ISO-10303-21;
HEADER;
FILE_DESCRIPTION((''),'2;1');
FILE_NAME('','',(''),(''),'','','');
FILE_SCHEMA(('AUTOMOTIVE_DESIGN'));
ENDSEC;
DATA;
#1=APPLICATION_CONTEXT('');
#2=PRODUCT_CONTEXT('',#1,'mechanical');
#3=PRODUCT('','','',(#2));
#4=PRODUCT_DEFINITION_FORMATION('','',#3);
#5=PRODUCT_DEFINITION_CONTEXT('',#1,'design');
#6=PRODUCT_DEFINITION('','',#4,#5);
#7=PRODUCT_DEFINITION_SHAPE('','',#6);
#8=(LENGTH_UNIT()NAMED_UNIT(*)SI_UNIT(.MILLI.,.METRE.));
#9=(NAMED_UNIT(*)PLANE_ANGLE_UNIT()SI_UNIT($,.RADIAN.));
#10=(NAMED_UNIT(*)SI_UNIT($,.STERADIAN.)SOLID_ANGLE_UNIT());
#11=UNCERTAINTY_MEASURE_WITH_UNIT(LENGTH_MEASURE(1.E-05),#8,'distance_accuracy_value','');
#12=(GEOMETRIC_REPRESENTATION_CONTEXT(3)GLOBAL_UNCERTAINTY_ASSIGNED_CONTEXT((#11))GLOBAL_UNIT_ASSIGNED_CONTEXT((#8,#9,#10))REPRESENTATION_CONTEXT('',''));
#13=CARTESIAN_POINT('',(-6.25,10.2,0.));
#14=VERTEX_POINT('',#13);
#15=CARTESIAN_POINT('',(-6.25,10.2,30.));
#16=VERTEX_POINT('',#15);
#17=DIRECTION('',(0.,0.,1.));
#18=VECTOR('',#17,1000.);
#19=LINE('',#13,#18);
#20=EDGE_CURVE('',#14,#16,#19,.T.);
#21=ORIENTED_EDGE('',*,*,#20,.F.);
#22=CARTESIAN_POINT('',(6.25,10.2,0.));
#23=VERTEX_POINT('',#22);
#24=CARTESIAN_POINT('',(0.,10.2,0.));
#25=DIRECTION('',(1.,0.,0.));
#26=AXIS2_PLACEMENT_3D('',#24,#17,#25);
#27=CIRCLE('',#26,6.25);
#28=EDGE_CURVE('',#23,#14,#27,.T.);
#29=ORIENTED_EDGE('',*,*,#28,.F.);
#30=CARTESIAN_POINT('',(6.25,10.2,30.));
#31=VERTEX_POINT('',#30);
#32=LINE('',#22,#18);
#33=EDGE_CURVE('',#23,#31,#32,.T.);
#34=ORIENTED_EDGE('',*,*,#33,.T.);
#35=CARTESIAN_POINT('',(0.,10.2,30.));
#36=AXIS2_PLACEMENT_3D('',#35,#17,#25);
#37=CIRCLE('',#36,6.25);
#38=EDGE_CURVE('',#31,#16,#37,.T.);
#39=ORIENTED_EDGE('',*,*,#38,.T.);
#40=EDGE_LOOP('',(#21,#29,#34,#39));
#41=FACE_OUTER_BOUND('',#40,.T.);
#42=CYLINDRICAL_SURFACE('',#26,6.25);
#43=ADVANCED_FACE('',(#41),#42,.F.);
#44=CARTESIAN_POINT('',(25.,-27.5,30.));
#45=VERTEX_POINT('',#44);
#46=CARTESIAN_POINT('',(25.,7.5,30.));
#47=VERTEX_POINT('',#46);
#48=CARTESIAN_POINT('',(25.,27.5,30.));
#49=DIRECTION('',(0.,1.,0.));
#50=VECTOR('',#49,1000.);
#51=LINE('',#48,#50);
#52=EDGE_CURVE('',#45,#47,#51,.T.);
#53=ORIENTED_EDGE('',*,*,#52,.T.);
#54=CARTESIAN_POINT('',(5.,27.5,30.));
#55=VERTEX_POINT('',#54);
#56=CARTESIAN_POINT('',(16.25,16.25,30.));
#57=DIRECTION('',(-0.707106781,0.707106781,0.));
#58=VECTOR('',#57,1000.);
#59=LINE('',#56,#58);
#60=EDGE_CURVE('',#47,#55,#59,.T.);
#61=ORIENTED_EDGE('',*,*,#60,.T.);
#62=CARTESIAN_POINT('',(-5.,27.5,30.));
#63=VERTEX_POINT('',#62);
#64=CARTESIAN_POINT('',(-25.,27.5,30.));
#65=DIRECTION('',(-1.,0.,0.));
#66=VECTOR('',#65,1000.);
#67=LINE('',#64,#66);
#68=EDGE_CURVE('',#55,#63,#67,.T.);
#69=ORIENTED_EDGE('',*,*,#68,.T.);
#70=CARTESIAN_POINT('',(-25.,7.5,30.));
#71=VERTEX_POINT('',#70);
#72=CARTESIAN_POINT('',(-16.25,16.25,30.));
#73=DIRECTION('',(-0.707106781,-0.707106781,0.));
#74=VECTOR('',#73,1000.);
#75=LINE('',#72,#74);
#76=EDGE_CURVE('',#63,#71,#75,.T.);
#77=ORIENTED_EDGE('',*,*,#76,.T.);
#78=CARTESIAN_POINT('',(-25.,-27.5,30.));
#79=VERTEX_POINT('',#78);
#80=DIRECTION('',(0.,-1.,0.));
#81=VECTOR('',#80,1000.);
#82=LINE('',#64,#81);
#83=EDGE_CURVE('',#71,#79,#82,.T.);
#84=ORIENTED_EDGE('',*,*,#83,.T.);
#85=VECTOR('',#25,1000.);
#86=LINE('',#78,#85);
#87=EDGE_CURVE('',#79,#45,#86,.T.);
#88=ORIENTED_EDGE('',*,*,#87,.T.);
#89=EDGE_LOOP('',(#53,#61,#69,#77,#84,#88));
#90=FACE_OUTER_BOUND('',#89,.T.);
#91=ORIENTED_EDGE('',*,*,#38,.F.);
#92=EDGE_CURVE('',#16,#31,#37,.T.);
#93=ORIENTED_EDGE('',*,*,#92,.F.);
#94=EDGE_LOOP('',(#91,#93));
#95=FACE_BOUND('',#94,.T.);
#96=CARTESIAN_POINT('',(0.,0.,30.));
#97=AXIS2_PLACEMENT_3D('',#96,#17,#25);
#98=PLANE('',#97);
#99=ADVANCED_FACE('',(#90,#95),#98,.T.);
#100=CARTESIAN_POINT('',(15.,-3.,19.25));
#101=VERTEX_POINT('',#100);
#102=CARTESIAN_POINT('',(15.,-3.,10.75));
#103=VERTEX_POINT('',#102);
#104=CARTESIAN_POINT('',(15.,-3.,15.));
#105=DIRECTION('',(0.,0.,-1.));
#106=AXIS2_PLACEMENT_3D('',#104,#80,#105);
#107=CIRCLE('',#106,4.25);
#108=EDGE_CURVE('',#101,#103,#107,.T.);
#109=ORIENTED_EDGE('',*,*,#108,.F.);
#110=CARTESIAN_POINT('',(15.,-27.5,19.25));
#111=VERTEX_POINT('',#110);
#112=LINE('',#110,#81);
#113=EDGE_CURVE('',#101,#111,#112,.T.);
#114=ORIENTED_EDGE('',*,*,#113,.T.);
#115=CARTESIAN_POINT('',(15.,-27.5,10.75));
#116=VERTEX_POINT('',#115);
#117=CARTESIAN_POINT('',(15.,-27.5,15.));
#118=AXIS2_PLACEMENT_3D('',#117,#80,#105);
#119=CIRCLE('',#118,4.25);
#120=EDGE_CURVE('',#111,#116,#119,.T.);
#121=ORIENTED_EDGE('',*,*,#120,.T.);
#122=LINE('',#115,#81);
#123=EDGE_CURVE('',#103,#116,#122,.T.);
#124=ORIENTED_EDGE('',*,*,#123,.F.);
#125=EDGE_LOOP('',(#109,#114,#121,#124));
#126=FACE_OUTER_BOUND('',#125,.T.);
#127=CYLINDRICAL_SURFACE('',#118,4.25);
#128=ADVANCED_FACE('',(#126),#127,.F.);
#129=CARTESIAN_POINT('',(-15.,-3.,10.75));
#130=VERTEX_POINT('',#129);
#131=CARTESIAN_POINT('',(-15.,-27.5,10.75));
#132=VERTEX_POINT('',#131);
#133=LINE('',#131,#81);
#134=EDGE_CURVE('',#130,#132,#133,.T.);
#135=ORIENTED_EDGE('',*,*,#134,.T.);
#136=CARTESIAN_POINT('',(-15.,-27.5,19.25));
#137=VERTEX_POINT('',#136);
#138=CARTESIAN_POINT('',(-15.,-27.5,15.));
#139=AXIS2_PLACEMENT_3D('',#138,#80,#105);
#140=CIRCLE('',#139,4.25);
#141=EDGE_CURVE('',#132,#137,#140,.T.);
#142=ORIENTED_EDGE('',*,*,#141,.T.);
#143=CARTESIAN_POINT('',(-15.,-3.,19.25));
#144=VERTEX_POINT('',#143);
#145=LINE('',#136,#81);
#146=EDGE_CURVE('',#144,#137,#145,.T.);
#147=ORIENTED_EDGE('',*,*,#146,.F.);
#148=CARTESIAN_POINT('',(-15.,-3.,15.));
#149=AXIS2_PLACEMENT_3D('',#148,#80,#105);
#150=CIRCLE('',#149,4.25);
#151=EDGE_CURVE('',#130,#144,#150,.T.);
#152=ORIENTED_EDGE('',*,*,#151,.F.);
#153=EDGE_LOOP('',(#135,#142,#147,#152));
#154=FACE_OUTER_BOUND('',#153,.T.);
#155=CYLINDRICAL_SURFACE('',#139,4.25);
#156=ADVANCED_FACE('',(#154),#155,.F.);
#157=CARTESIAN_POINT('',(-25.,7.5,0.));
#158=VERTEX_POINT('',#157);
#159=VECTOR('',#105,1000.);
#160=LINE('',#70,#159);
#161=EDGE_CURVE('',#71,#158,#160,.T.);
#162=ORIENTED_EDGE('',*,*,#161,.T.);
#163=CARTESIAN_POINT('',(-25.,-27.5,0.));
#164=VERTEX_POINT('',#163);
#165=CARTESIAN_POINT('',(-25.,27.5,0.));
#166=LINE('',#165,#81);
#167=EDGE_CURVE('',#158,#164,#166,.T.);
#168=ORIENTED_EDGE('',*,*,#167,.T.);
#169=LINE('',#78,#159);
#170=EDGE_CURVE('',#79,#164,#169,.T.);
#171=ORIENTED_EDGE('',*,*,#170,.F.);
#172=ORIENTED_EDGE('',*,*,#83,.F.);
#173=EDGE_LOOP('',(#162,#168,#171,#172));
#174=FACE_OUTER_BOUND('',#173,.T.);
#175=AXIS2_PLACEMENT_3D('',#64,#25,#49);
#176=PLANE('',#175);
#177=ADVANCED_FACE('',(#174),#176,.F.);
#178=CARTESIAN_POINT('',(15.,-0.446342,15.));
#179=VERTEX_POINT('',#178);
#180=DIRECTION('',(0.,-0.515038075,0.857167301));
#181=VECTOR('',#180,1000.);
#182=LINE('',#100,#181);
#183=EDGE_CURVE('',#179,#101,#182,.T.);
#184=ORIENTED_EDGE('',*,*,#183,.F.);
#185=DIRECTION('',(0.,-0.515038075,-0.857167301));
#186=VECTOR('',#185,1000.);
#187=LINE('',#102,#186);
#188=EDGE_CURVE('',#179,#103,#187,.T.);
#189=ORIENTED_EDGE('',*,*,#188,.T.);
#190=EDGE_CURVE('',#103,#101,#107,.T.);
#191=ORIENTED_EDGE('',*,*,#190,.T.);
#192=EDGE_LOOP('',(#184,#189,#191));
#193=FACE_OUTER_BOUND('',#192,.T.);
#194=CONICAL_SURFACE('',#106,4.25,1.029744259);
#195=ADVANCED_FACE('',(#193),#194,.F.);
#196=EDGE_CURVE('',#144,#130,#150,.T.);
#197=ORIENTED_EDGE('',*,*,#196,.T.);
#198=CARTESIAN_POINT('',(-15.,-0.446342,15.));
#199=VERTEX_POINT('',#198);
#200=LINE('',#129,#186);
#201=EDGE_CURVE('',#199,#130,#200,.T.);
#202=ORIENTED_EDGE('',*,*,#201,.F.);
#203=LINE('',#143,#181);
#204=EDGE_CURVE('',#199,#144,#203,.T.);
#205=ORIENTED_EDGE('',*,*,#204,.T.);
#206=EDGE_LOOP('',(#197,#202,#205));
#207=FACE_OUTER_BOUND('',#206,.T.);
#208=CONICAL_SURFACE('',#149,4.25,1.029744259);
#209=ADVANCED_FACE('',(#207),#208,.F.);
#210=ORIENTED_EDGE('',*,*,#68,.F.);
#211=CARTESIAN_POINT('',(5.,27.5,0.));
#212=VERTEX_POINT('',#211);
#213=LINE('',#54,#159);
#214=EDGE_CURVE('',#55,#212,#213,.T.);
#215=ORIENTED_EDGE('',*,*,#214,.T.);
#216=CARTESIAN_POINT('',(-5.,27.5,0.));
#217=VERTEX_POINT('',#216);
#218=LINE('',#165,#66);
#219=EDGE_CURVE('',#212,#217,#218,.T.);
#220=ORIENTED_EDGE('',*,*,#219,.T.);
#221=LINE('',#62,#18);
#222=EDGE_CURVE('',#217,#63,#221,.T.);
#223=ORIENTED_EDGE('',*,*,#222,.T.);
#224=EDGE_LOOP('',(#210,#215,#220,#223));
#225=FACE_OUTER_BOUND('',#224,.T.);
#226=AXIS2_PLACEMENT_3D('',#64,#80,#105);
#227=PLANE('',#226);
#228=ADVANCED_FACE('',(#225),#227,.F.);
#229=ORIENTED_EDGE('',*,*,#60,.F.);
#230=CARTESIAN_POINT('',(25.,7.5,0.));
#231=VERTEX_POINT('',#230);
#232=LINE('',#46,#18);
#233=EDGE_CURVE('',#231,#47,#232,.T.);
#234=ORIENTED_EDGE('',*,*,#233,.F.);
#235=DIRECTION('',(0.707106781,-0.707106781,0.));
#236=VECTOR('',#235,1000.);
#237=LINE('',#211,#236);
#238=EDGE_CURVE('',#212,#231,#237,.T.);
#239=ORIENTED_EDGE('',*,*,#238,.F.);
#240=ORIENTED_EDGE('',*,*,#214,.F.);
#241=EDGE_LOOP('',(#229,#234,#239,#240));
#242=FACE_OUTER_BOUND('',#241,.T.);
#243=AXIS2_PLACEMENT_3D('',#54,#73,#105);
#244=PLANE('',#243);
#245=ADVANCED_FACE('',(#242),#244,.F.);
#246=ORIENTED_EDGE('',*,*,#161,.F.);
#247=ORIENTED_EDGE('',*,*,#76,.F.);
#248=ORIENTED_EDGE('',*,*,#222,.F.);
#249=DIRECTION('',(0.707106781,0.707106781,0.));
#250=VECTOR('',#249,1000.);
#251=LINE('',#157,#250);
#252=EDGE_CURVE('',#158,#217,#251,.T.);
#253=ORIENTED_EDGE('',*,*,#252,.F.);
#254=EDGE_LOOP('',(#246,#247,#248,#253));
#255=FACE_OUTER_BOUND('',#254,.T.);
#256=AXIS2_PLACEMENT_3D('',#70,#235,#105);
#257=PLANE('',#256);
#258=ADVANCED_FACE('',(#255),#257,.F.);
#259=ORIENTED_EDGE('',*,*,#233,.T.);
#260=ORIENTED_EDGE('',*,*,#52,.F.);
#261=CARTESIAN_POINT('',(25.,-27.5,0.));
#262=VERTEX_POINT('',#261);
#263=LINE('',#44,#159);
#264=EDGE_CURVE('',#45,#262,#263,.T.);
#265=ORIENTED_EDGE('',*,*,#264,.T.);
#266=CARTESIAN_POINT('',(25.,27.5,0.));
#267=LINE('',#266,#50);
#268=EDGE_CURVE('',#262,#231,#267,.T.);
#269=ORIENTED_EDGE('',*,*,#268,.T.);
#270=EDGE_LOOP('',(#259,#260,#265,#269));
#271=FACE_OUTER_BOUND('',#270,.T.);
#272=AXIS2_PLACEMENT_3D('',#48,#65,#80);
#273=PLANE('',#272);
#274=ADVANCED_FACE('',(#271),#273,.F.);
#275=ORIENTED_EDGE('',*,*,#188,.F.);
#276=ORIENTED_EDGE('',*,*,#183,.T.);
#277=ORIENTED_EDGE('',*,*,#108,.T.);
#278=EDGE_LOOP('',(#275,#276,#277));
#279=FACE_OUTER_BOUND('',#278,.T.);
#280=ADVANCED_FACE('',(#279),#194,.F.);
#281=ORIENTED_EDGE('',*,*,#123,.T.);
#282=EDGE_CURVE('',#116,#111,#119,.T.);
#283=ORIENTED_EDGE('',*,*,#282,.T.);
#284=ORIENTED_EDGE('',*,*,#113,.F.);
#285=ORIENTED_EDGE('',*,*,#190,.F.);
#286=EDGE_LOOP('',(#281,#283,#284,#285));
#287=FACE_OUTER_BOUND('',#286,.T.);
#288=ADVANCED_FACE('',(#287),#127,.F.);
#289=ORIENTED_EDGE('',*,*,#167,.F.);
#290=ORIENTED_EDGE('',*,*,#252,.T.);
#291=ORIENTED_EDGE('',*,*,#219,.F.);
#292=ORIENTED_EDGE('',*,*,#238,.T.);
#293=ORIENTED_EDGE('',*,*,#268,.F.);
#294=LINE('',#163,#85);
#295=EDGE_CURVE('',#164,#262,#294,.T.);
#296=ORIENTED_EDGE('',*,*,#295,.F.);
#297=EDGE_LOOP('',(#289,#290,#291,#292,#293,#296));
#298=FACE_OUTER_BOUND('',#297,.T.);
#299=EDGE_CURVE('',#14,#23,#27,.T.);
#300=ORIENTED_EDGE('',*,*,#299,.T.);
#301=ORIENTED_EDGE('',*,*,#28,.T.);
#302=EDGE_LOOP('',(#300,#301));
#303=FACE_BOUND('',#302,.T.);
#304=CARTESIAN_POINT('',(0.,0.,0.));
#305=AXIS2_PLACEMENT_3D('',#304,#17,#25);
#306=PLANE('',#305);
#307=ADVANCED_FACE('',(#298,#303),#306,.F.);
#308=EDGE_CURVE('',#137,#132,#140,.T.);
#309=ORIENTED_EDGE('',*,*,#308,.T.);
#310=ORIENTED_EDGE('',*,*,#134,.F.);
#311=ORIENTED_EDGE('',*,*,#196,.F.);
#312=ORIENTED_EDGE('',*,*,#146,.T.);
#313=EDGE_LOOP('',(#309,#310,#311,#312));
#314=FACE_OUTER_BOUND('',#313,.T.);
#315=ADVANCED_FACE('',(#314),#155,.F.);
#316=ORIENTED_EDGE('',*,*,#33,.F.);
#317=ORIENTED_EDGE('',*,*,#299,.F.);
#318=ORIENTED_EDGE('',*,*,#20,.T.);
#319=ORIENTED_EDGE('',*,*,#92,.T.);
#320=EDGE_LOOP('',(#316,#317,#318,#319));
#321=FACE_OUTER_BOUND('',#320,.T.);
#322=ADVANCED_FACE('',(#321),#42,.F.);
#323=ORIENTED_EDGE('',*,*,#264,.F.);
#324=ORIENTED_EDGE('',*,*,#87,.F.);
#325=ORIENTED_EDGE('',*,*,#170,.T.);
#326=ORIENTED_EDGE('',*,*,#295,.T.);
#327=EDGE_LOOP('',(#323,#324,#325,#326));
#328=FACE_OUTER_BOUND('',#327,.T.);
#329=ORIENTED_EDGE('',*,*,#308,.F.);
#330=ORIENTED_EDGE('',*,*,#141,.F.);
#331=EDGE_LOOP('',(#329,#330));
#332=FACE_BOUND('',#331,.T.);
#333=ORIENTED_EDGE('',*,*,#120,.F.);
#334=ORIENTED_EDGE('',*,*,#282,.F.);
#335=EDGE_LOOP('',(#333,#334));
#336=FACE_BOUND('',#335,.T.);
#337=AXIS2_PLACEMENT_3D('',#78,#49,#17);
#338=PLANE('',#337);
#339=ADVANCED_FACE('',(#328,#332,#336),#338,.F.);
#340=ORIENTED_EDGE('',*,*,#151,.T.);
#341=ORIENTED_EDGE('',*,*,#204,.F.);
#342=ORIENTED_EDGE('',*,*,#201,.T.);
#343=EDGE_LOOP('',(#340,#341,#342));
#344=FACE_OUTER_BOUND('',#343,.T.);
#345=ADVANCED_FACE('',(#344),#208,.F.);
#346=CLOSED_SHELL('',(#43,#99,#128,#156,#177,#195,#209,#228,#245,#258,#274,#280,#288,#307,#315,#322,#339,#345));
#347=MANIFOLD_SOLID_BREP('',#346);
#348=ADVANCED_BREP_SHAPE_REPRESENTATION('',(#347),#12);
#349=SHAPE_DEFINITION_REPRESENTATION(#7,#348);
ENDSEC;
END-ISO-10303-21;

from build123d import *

# Parameters (mm, degrees)
SKETCH_1_W              = 50
SKETCH_1_H              = 55
EXTRUDE_1_DEPTH         = 30
CHAMFER_1_SIZE          = 20
HOLE_WIZARD_M10_1_D     = 8.5
HOLE_WIZARD_M10_1_DEPTH = 24.5
HOLE_WIZARD_M10_1_TIP   = 2.553657631
SKETCH_5_R              = 6.25
CUT_EXTRUDE_1_DEPTH     = 30


with BuildPart() as part:
    # 草图1 → 凸台-拉伸1 (new body)
    with BuildSketch(Plane.XY):
        Rectangle(SKETCH_1_W, SKETCH_1_H)
    extrude(amount=EXTRUDE_1_DEPTH)

    # 倒角1
    chamfer_1_edges = [part.edges().sort_by_distance(p)[0] for p in [
        (-25, 27.5, 15),
        (25, 27.5, 15),
    ]]
    chamfer(chamfer_1_edges, length=CHAMFER_1_SIZE)

    # M10 螺纹孔1
    with Locations(Plane(origin=(0, -27.5, 0), x_dir=(-1, 0, 0), z_dir=(0, -1, 0))):
        with Locations((15, -15), (-15, -15)):
            Hole(HOLE_WIZARD_M10_1_D / 2, depth=HOLE_WIZARD_M10_1_DEPTH)
            with Locations((0, 0, -(HOLE_WIZARD_M10_1_DEPTH + HOLE_WIZARD_M10_1_TIP / 2))):  # 118° drill point
                Cone(0, HOLE_WIZARD_M10_1_D / 2, HOLE_WIZARD_M10_1_TIP, mode=Mode.SUBTRACT)

    # 草图5 → 切除-拉伸1 (cut)
    with BuildSketch(Plane.XY.offset(30)):
        with Locations((0, 10.2)):
            Circle(SKETCH_5_R)
    extrude(amount=-CUT_EXTRUDE_1_DEPTH, mode=Mode.SUBTRACT)


solid = part.part
